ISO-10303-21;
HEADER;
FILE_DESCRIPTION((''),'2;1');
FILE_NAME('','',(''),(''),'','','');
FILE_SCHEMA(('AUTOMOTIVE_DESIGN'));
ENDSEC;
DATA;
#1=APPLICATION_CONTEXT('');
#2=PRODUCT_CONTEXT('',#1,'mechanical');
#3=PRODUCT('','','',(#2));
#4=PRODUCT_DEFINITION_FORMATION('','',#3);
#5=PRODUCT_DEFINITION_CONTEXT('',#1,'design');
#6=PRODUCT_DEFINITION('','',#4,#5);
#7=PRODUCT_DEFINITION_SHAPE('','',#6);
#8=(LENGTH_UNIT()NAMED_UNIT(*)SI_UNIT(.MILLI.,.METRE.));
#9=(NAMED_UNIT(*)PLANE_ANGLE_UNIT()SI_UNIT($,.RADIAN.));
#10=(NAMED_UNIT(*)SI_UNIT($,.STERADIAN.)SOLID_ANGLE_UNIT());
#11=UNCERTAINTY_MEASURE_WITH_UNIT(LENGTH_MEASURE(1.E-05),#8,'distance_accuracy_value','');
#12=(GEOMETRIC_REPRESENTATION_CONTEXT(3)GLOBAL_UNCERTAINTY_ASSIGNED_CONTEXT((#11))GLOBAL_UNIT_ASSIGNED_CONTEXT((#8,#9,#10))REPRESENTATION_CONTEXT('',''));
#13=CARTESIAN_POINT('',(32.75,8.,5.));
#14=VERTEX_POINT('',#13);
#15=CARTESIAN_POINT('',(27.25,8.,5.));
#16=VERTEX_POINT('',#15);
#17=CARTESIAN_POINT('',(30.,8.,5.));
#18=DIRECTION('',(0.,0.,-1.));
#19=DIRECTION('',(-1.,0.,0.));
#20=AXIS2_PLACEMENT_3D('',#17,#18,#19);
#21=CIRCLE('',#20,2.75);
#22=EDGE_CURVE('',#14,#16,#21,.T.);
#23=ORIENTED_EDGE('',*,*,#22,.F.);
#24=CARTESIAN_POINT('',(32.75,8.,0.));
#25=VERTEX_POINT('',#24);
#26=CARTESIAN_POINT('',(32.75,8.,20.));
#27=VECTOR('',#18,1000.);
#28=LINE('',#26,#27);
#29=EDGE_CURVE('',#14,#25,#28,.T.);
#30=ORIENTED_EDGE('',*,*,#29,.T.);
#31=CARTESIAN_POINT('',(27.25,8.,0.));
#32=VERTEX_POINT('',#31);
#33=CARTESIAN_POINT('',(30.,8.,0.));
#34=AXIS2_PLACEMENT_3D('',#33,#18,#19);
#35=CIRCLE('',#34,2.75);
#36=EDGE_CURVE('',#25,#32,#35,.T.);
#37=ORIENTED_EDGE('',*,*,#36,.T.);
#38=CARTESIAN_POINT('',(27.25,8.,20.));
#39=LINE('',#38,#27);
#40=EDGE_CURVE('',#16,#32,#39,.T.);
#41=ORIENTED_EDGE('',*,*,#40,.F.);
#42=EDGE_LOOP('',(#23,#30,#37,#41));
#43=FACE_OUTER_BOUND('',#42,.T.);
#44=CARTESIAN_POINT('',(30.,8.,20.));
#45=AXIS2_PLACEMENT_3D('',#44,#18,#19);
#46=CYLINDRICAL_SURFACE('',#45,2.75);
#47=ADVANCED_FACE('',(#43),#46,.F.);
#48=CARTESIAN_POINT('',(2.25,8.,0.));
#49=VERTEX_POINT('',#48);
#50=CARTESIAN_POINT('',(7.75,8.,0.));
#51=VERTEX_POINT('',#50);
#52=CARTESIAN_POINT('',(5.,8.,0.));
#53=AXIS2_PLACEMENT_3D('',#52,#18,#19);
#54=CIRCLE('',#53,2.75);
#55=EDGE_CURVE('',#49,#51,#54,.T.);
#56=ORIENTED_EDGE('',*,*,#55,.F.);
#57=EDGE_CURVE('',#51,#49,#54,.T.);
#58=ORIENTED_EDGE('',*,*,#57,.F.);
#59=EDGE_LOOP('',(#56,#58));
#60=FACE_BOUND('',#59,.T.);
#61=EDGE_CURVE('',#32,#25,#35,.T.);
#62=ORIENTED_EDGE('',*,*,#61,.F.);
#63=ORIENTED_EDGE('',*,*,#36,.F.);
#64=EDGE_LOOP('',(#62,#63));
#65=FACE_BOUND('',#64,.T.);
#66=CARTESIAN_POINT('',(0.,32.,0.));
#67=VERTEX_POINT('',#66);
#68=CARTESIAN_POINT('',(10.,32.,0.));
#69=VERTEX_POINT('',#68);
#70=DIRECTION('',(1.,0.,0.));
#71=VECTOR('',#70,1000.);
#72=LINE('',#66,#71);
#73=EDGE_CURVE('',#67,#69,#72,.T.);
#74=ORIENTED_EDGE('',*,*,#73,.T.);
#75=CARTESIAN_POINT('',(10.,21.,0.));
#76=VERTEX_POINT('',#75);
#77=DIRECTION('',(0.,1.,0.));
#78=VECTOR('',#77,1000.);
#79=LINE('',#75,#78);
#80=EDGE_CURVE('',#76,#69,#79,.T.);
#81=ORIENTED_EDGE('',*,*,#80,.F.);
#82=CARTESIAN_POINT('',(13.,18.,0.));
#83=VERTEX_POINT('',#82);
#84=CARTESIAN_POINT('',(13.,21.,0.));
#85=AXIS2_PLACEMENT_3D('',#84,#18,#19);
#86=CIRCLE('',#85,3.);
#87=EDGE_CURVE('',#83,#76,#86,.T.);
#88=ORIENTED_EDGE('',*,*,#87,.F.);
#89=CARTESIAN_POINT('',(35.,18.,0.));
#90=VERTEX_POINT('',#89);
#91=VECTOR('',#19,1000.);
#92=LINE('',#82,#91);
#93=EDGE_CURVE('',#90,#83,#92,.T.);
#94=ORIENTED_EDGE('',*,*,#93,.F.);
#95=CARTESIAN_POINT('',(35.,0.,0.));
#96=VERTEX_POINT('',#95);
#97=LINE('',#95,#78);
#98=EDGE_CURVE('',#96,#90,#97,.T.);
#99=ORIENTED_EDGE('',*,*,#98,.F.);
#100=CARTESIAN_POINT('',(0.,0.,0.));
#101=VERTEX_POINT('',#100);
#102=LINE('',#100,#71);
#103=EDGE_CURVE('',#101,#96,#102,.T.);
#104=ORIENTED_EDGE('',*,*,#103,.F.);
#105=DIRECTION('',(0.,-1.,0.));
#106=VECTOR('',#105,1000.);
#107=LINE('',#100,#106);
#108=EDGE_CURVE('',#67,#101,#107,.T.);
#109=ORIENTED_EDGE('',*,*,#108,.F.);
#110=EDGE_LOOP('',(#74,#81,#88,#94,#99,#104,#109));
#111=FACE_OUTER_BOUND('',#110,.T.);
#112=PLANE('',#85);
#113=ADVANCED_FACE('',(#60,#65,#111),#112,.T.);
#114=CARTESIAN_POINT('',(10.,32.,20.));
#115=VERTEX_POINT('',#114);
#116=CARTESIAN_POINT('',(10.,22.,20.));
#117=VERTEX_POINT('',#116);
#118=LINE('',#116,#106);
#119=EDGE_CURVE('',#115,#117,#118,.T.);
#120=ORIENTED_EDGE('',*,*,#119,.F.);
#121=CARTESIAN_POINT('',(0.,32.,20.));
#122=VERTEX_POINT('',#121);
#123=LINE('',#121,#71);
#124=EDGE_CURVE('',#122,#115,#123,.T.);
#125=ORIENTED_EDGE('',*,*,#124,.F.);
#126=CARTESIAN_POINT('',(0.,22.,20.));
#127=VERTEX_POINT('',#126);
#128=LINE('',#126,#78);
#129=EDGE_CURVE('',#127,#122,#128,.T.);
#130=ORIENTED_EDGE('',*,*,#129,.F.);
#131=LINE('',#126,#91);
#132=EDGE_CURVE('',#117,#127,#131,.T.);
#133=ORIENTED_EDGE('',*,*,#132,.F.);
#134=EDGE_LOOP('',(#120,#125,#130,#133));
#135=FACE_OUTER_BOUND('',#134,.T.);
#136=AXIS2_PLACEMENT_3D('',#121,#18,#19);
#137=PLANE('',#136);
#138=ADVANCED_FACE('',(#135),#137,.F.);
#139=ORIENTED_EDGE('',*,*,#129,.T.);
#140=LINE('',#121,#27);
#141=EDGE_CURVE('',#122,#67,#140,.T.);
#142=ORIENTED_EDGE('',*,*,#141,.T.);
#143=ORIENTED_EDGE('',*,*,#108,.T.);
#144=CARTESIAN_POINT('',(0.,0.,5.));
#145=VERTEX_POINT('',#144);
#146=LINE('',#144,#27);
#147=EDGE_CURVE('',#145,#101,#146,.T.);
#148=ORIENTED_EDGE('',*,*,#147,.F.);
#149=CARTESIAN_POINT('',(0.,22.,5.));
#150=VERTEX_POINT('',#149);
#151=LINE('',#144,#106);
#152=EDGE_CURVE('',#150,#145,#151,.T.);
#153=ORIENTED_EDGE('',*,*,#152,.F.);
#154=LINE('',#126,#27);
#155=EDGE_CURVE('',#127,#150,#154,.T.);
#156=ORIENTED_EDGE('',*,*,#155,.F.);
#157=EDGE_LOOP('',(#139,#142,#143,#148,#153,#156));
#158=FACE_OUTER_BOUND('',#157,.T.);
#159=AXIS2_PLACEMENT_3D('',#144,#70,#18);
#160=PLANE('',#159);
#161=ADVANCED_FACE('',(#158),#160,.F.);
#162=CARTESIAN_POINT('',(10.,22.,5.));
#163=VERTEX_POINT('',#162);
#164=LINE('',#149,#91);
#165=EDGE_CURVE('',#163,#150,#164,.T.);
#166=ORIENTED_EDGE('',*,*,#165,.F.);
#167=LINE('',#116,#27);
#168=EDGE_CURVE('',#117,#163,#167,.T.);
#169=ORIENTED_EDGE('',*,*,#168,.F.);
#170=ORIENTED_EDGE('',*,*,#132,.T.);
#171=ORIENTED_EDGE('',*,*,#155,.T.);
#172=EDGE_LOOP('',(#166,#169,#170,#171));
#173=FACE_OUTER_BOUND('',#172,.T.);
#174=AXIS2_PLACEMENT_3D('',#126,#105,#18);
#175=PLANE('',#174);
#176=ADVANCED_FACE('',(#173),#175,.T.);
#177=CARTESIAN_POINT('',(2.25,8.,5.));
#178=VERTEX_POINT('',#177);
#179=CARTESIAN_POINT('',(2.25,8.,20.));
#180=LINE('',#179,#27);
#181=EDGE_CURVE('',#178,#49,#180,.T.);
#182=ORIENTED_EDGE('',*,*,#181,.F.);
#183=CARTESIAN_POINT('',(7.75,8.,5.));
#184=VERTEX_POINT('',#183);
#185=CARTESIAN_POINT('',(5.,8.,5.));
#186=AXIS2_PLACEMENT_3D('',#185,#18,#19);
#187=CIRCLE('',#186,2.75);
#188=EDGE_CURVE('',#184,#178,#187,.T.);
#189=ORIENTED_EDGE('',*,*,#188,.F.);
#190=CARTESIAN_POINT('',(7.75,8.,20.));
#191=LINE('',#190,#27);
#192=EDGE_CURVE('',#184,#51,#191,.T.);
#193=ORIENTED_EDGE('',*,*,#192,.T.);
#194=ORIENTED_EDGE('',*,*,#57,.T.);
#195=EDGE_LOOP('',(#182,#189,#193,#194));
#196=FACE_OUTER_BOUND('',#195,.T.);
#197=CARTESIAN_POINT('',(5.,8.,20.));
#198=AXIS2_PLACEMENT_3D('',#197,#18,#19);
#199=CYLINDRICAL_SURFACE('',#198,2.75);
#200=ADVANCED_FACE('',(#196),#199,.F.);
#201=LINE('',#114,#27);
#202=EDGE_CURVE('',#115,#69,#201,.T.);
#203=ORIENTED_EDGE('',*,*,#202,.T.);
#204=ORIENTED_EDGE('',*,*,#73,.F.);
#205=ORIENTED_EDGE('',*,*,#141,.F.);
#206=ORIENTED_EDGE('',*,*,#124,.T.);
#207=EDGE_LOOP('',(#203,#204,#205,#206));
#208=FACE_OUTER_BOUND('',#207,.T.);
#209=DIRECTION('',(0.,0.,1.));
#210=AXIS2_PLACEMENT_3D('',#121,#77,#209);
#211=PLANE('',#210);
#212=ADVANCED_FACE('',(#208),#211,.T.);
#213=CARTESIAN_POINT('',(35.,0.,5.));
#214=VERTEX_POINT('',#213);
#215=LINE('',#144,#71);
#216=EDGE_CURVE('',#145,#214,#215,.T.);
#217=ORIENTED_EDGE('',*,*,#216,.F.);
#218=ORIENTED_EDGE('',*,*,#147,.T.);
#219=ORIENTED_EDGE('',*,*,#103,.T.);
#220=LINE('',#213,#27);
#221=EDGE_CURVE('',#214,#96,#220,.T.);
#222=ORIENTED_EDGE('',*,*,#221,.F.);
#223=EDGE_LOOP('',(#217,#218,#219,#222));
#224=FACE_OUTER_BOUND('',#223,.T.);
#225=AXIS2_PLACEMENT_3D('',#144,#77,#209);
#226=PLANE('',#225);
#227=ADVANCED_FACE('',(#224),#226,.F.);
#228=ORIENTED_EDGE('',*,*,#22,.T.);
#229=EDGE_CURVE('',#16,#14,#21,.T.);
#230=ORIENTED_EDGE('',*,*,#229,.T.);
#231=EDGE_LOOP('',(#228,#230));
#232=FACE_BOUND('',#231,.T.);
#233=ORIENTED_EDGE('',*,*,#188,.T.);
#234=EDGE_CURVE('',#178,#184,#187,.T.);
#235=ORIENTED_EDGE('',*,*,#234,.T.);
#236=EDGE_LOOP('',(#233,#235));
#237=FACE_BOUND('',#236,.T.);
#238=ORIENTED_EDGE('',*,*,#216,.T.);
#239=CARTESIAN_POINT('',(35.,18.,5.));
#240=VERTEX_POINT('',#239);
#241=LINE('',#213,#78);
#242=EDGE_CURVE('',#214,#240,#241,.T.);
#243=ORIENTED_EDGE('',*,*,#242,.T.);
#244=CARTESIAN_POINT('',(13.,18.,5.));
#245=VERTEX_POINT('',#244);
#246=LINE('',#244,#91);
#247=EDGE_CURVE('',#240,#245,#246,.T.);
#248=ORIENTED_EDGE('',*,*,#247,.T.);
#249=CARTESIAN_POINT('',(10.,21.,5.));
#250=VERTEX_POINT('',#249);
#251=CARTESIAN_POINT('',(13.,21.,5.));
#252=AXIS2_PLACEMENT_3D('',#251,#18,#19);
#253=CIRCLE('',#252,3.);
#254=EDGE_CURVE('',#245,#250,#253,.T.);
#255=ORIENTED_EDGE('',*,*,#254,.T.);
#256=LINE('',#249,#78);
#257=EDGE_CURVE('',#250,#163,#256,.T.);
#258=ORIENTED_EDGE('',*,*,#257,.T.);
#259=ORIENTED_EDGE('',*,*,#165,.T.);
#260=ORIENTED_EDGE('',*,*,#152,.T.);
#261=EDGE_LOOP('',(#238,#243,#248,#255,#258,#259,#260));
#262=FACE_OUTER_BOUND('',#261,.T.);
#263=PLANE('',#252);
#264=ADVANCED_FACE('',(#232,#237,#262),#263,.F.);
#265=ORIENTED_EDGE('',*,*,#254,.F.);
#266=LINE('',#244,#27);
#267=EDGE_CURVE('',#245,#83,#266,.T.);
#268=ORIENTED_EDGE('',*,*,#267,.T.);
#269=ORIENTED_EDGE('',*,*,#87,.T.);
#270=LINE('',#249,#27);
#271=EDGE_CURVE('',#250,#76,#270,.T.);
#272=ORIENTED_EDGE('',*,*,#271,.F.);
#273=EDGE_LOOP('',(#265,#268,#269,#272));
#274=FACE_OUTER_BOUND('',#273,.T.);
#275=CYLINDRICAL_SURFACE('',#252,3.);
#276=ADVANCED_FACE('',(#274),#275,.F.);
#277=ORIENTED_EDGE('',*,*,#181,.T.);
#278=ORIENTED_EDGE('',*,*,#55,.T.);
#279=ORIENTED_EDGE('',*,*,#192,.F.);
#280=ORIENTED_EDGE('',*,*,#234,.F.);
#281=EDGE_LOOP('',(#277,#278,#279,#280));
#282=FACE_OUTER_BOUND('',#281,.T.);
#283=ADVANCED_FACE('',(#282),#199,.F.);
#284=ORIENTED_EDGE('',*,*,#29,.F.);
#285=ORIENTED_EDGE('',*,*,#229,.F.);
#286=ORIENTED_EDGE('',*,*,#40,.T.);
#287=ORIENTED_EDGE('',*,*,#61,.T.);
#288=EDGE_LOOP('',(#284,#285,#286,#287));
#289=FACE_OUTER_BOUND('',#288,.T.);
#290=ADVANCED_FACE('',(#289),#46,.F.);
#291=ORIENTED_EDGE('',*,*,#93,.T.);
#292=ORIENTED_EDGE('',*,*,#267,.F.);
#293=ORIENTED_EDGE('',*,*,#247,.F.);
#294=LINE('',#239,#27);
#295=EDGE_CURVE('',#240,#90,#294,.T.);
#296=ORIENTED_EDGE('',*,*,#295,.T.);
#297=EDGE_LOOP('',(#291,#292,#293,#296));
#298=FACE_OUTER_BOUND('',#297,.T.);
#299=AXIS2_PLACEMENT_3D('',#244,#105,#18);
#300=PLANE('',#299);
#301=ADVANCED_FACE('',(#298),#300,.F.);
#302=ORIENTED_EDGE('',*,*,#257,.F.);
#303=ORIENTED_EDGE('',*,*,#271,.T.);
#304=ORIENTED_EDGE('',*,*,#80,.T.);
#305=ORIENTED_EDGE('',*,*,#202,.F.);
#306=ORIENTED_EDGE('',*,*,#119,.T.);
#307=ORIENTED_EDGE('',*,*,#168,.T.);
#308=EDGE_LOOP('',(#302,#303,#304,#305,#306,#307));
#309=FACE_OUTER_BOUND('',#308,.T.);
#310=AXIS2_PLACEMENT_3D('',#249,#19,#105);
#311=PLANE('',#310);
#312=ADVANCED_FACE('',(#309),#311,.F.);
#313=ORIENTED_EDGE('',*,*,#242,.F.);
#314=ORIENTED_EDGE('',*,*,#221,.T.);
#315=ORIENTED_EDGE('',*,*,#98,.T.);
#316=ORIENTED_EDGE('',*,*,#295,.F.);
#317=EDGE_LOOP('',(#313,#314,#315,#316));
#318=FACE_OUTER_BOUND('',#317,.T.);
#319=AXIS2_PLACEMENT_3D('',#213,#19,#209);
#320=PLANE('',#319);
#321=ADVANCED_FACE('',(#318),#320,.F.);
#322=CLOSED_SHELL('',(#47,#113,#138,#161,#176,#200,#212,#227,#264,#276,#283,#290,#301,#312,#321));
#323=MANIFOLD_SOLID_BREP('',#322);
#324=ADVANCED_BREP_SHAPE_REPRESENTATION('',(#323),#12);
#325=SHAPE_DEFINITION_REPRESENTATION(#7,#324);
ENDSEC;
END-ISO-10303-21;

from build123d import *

# Parameters (mm, degrees)
EXTRUDE_1_DEPTH     = 5
SKETCH_5_W          = 10
SKETCH_5_H          = 10
EXTRUDE_3_DEPTH     = 20
SKETCH_4_R          = 2.75
CUT_EXTRUDE_1_DEPTH = 20


with BuildPart() as part:
    # 草图1 → 凸台-拉伸1 (new body)
    with BuildSketch(Plane.XY):
        with BuildLine():
            Line((0, 0), (35, 0))
            Line((35, 0), (35, 18))
            Line((35, 18), (13, 18))
            ThreePointArc((13, 18), (10.878679656, 18.878679656), (10, 21))
            Line((10, 21), (10, 22))
            Line((10, 22), (0, 22))
            Line((0, 22), (0, 0))
        make_face()
    extrude(amount=EXTRUDE_1_DEPTH)

    # 草图5 → 凸台-拉伸3 (add)
    with BuildSketch(Plane(origin=(0, 0, 0), x_dir=(-1, 0, 0), z_dir=(0, 0, -1))):
        with Locations((-5, 27)):
            Rectangle(SKETCH_5_W, SKETCH_5_H)
    extrude(amount=-EXTRUDE_3_DEPTH)

    # 草图4 → 切除-拉伸1 (cut)
    with BuildSketch(Plane(origin=(0, 0, 0), x_dir=(-1, 0, 0), z_dir=(0, 0, -1))):
        with Locations((-30, 8)):
            Circle(SKETCH_4_R)
        with Locations((-5, 8)):
            Circle(SKETCH_4_R)
    extrude(amount=-CUT_EXTRUDE_1_DEPTH, mode=Mode.SUBTRACT)


solid = part.part
